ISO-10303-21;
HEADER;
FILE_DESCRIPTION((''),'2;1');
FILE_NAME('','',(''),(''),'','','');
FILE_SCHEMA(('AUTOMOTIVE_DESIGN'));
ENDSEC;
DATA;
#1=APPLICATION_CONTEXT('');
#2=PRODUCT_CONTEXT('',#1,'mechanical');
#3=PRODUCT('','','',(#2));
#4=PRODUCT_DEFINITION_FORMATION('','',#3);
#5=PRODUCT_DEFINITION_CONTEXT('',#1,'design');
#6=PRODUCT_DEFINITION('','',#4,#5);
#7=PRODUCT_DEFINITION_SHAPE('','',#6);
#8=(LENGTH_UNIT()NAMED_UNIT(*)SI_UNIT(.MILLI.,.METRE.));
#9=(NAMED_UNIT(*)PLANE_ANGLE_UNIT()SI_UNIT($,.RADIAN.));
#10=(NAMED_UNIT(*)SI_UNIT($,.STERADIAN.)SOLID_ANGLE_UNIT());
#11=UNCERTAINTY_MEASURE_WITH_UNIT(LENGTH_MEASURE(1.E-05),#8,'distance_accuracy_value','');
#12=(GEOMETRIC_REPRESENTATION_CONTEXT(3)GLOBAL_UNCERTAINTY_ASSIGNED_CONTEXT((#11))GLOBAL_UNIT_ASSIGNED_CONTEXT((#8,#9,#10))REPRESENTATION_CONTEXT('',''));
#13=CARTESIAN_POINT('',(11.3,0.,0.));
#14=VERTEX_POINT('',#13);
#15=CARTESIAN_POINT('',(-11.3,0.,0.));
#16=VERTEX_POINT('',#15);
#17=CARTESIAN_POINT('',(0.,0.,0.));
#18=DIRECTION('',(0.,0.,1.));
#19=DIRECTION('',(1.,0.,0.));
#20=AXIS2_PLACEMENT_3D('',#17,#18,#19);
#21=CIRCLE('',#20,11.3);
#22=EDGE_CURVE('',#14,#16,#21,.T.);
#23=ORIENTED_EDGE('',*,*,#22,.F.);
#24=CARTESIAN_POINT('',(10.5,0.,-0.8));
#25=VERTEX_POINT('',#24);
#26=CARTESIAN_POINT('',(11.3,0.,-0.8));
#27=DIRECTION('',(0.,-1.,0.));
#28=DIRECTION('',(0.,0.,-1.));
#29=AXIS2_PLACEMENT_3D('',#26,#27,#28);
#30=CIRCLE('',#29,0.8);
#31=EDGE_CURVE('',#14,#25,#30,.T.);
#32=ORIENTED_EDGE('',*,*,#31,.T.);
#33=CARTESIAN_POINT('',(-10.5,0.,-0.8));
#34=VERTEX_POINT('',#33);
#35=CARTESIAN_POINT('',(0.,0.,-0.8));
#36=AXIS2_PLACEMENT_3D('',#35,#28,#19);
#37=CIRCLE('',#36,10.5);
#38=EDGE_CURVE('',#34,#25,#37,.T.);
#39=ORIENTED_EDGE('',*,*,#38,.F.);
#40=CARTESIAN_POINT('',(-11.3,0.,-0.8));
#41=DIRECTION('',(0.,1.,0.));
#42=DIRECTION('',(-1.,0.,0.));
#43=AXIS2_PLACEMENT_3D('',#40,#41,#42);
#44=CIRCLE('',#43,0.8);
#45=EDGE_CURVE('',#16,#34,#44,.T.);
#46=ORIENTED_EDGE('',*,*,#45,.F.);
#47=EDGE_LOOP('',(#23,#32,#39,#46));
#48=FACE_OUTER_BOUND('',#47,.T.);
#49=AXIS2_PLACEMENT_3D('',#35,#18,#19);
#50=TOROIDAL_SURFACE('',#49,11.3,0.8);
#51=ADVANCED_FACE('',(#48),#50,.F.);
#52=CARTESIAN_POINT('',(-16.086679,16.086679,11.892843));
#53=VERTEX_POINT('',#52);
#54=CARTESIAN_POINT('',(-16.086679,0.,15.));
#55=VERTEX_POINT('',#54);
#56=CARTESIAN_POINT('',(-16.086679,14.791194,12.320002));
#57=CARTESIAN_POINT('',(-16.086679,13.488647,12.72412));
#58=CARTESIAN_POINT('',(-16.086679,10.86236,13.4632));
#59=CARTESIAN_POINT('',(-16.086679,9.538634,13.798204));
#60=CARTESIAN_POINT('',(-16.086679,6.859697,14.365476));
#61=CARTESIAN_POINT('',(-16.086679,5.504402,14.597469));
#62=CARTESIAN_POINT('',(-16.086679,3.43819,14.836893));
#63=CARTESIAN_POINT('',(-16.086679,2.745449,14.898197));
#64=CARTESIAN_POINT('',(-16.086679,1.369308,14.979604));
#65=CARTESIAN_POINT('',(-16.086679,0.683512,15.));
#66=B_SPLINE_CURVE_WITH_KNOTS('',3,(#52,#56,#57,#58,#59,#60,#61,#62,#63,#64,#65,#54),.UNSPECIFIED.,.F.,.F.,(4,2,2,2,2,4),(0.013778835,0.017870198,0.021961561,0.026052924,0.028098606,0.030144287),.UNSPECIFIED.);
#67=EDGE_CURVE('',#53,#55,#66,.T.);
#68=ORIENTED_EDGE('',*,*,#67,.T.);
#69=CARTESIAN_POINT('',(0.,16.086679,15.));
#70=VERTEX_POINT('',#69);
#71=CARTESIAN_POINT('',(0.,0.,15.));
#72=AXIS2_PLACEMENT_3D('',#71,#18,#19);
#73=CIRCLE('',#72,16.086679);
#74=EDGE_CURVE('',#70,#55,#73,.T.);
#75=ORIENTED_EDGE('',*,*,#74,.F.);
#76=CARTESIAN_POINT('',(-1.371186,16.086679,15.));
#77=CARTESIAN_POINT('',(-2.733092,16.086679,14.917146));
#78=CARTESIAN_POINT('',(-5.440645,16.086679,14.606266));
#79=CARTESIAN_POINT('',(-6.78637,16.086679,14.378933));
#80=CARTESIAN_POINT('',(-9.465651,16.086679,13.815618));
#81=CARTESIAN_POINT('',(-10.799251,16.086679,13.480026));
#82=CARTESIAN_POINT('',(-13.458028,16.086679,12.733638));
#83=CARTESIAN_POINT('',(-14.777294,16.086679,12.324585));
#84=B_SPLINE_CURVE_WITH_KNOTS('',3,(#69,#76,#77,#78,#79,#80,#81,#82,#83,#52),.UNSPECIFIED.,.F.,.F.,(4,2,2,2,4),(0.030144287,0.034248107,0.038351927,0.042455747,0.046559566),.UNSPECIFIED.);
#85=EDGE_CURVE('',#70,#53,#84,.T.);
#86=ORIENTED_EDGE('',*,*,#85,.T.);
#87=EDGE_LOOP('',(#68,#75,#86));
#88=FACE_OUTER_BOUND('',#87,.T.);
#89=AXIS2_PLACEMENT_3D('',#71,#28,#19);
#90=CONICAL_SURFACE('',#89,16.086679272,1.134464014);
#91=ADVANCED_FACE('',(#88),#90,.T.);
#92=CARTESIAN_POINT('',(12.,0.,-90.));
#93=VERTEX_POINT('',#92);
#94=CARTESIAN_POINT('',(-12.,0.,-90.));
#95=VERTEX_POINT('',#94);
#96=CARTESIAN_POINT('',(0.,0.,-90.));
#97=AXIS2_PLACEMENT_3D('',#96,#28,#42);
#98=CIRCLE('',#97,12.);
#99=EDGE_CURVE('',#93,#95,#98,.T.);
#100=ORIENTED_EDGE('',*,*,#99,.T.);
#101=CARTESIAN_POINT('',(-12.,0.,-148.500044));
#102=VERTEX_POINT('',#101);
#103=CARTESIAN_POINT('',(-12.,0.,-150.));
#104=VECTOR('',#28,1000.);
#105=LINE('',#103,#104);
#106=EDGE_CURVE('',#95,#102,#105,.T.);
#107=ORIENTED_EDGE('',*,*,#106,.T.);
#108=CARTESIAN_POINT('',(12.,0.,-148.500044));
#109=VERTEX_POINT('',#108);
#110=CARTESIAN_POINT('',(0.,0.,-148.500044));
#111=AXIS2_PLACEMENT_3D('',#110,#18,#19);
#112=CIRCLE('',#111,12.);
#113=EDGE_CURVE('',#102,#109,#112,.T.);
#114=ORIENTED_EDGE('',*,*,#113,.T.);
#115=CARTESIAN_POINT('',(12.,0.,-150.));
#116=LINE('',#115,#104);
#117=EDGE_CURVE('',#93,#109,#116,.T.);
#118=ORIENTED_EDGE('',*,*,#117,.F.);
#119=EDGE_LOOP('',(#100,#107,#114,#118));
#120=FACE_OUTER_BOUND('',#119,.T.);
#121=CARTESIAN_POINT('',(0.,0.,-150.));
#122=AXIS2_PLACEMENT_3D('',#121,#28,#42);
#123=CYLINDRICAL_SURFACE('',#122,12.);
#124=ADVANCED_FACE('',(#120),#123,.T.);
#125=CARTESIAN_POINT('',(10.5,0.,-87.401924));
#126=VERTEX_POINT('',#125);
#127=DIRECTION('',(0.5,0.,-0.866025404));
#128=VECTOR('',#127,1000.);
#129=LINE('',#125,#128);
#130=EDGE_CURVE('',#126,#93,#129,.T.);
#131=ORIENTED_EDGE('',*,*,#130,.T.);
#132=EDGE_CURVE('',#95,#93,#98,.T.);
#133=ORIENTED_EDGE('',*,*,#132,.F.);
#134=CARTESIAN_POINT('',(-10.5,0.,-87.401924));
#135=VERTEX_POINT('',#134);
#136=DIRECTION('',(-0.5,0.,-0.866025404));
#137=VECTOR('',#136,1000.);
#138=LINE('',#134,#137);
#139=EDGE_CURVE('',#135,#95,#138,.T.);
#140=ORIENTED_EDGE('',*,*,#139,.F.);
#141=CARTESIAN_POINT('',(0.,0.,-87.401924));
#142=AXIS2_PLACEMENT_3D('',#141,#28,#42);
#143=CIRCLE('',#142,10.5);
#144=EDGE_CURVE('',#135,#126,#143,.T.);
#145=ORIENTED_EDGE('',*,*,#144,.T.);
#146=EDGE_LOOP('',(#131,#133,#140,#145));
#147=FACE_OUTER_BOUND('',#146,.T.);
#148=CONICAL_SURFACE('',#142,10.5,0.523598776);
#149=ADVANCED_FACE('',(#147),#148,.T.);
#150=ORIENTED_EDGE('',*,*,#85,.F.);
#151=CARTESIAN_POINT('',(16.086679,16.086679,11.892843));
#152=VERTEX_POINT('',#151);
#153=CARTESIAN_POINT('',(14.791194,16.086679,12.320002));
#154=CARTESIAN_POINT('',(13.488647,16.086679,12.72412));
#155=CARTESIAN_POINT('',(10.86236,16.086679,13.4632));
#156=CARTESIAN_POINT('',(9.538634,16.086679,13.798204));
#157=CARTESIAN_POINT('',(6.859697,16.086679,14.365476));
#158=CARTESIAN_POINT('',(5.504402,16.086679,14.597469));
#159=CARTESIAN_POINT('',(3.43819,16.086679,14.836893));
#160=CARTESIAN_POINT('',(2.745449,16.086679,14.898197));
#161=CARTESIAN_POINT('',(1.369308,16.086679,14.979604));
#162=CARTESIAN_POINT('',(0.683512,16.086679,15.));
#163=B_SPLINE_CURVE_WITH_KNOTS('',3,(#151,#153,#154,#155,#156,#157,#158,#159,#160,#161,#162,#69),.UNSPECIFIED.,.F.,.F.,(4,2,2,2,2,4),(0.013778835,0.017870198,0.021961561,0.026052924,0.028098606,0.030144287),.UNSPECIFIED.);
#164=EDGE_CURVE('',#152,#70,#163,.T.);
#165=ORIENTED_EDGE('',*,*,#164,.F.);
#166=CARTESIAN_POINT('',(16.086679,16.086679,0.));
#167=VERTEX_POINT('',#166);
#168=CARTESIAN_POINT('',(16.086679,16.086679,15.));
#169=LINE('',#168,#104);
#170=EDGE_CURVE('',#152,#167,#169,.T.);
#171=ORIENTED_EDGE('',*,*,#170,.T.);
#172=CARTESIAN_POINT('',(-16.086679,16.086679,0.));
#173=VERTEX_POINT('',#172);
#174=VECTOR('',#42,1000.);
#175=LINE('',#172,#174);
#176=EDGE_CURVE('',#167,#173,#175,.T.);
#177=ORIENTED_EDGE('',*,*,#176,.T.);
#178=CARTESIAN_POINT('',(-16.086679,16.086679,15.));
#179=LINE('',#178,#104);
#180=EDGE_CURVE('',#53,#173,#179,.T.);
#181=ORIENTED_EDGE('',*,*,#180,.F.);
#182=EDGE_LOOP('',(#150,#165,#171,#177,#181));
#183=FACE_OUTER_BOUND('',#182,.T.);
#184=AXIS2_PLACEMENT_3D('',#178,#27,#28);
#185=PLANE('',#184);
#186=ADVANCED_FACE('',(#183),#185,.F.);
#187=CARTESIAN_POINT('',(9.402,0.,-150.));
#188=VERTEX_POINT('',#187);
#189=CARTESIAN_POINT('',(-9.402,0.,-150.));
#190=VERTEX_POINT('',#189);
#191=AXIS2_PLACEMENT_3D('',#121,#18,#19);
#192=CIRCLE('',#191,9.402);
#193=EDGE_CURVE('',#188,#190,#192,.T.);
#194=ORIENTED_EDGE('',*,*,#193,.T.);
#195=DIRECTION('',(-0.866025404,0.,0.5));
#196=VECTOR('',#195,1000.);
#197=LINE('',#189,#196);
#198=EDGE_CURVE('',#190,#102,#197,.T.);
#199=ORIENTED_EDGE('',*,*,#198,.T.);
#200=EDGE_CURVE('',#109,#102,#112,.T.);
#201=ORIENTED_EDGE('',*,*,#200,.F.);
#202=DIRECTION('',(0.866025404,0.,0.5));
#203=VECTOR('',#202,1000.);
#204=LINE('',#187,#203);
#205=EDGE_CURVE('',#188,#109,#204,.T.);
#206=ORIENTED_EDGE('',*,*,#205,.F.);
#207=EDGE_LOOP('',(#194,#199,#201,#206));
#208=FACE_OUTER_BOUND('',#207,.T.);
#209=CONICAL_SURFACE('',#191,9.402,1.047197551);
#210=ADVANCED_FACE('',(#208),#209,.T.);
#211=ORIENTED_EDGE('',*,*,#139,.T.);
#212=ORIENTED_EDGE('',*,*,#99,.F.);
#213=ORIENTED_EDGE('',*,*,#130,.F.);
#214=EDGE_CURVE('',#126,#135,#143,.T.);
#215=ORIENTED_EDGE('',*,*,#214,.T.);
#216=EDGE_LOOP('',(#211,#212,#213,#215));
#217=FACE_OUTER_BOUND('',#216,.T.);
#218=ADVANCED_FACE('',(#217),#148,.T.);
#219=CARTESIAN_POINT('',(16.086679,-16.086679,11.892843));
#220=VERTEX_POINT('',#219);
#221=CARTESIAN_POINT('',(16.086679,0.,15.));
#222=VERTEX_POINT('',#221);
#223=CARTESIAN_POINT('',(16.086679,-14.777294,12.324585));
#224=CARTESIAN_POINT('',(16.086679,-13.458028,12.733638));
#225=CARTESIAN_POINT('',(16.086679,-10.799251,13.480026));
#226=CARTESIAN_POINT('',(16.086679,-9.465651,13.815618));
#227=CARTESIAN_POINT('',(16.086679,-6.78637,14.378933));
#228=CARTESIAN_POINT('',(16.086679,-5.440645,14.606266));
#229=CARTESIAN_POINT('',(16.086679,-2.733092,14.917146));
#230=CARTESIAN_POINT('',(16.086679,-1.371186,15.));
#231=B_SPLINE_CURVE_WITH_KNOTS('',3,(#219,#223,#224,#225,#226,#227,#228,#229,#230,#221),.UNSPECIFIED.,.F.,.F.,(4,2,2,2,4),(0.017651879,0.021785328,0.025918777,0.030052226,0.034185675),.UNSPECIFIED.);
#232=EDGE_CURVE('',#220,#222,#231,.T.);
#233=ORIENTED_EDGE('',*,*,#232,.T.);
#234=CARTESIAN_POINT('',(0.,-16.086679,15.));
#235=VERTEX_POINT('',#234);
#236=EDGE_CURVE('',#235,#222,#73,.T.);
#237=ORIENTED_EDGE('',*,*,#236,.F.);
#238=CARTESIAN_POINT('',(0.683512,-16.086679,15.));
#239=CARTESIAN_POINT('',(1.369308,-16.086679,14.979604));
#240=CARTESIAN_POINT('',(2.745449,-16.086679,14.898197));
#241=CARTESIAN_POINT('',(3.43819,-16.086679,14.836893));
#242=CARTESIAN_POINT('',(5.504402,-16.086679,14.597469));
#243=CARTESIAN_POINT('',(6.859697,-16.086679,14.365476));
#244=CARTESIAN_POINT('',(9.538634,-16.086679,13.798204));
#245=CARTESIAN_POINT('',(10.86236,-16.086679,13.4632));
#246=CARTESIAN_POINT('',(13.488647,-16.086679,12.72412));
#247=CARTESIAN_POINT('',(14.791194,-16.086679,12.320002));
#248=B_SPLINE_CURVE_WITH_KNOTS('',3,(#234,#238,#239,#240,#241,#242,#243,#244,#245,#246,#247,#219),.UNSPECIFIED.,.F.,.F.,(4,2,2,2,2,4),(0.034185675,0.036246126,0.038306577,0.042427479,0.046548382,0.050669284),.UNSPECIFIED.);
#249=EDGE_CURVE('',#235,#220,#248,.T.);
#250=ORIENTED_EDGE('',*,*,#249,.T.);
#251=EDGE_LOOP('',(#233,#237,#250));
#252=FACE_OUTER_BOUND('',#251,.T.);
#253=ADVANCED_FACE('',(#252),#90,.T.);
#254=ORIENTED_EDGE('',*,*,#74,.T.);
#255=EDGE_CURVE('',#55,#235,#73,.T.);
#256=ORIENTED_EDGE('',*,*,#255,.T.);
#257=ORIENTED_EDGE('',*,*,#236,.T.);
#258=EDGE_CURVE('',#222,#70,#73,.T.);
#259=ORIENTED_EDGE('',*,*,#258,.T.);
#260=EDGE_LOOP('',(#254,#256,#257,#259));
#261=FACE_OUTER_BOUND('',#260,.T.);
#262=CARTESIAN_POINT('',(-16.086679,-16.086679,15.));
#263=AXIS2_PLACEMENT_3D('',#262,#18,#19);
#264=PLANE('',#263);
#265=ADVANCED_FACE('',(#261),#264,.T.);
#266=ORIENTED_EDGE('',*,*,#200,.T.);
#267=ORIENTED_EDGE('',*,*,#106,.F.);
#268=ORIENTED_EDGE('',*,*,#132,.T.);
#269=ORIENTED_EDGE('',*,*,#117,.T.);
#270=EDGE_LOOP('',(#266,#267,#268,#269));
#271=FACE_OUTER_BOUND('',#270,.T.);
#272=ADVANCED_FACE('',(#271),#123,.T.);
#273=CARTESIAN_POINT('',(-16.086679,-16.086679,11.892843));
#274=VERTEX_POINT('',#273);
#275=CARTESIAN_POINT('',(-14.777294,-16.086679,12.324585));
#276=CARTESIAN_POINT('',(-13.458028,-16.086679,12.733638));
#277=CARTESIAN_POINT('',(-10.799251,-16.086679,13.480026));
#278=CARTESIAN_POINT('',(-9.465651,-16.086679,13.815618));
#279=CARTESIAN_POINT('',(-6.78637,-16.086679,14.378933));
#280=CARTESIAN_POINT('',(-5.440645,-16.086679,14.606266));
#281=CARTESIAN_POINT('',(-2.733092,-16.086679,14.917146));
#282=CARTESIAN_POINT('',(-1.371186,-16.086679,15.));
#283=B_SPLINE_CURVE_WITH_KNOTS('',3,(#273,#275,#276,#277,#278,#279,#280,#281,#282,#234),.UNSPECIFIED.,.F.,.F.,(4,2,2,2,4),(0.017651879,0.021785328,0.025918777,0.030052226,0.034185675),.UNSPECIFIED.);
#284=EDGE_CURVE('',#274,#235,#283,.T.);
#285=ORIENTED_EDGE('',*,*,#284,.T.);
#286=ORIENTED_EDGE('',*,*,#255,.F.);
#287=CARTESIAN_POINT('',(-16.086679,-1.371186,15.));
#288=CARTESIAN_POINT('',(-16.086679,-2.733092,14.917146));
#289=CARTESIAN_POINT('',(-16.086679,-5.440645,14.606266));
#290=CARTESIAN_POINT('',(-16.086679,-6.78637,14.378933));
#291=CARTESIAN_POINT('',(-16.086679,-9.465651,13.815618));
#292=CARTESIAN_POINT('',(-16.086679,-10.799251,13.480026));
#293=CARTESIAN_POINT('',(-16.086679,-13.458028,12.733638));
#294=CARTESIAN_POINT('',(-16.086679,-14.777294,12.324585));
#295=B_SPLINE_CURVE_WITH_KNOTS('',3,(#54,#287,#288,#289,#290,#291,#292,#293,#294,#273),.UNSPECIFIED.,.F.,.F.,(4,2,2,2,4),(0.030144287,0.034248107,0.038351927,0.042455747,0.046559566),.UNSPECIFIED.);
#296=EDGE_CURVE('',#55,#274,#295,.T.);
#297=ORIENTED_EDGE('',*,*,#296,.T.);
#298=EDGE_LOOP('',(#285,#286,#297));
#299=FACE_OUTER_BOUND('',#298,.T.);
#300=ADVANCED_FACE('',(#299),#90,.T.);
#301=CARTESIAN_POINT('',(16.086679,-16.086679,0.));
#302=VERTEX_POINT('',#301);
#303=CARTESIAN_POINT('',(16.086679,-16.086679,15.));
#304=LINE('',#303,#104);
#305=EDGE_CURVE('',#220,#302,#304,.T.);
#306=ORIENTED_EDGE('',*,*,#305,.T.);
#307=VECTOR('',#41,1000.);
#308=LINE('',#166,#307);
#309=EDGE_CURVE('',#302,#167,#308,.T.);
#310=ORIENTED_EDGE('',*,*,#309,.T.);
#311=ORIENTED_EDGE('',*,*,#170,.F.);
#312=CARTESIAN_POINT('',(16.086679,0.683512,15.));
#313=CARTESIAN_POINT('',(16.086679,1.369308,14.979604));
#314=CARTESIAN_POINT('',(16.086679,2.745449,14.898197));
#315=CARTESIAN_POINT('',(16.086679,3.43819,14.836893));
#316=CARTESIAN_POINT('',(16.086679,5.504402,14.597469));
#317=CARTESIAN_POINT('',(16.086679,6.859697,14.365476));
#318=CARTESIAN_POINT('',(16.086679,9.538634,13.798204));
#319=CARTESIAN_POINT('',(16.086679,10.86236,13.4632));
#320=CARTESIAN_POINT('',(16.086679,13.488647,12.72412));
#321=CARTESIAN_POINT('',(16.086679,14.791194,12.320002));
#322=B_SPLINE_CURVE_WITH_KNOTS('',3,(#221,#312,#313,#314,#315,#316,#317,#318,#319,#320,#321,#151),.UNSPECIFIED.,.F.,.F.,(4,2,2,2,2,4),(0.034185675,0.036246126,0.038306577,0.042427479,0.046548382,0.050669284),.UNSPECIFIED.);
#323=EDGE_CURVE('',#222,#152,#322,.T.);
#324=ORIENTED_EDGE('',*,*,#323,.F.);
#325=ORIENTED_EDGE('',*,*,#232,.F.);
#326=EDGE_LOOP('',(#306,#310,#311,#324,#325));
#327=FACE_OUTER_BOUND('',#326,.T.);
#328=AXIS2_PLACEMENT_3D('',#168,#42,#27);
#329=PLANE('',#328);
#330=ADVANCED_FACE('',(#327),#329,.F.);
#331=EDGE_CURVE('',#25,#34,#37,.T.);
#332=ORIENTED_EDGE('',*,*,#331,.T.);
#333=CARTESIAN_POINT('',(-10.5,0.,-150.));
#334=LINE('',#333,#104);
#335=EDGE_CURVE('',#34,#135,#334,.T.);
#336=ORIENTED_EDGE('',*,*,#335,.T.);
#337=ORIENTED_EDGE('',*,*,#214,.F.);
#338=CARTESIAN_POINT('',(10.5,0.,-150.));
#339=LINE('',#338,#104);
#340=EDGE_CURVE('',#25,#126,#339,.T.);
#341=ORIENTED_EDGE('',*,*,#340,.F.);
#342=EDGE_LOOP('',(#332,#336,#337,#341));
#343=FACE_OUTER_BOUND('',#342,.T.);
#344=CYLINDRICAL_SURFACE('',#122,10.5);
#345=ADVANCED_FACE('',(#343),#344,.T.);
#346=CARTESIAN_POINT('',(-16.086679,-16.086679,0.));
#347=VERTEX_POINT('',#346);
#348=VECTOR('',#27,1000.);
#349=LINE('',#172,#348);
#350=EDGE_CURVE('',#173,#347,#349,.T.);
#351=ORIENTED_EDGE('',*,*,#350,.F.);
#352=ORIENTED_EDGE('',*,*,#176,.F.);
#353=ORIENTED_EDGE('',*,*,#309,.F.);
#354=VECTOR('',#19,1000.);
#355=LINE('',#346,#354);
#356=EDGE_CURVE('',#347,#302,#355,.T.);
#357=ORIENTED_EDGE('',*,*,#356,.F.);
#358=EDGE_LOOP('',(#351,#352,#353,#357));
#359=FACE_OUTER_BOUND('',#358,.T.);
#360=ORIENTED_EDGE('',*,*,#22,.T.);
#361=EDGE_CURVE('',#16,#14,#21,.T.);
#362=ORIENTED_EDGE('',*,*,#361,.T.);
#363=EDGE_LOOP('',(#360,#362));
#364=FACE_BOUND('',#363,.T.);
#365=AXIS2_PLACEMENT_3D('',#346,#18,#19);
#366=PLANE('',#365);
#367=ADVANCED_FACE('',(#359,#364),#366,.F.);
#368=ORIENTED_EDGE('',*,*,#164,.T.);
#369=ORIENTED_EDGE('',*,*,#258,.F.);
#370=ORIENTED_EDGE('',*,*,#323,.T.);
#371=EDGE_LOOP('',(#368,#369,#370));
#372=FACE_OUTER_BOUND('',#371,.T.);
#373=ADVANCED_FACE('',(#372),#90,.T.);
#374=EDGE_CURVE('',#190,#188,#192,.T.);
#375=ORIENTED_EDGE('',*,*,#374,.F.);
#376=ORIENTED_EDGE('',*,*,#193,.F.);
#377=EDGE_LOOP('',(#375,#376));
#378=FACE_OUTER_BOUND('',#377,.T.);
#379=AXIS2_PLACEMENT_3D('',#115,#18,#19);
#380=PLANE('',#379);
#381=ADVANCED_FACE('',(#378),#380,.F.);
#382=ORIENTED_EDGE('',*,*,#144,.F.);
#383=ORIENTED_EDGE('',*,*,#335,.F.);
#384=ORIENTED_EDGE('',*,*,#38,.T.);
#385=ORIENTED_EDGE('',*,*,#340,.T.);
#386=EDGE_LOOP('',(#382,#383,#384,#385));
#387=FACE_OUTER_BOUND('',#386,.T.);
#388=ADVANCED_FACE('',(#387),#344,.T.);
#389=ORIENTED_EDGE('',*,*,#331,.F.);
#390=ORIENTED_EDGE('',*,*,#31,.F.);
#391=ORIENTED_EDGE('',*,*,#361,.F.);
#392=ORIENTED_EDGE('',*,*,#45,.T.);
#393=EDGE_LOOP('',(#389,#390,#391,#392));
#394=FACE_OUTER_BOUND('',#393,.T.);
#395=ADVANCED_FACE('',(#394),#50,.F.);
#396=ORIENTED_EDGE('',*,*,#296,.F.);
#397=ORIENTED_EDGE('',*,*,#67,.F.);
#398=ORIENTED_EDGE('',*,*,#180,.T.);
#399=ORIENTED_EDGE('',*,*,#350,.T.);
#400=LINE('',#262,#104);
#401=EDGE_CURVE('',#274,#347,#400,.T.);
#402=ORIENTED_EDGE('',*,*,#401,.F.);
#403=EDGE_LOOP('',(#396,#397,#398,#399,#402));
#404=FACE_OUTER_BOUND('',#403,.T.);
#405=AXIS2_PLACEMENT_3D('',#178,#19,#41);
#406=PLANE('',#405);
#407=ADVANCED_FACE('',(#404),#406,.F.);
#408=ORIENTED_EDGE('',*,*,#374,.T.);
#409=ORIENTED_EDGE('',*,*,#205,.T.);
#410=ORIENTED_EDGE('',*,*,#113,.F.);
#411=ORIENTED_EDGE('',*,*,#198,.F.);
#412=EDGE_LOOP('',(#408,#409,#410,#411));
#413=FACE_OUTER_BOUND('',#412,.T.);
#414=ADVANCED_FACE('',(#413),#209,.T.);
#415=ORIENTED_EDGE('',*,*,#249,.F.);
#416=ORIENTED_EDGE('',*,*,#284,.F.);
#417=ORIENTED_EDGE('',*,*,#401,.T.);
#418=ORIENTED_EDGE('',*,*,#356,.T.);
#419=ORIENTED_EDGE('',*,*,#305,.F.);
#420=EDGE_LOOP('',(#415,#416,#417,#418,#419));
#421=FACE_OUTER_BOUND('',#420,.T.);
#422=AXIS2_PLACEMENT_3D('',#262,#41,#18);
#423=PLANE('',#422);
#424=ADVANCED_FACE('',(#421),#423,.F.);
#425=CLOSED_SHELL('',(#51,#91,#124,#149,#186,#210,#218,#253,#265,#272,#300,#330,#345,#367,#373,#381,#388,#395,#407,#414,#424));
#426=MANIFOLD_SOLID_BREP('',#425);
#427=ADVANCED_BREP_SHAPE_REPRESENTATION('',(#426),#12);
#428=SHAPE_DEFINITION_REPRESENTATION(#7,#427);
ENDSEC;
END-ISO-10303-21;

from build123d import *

# Parameters (mm, degrees)
SKETCH1_W          = 32.173358544
SKETCH1_H          = 32.173358544
BASE_EXTRUDE_DEPTH = 15
SKETCH4_OUTSIDE_W  = 164.92
SKETCH4_OUTSIDE_H  = 164.92
SKETCH4_OUTSIDE_R  = 16.086679272
CUT_EXTRUDE1_DEPTH = 28.25
CUT_EXTRUDE1_DRAFT = -65
FILLET1_R          = 0.8


with BuildPart() as part:
    # Sketch1 → Base-Extrude (new body)
    with BuildSketch(Plane.XY):
        Rectangle(SKETCH1_W, SKETCH1_H)
    extrude(amount=BASE_EXTRUDE_DEPTH)


with BuildPart() as cut_extrude1_tool:
    # Sketch4 outside → Cut-Extrude1 (with draft: the straight prism first)
    with BuildSketch(Plane.XY.offset(15)):
        Rectangle(SKETCH4_OUTSIDE_W, SKETCH4_OUTSIDE_H)
        Circle(SKETCH4_OUTSIDE_R, mode=Mode.SUBTRACT)
    extrude(amount=-CUT_EXTRUDE1_DEPTH)
    # Cut-Extrude1: the draft: its side faces are tilted about the plane it starts from
    cut_extrude1_sides = [cut_extrude1_tool.faces().sort_by_distance(p)[0] for p in [
        (0, -82.46, 0.875),
        (82.46, 0, 0.875),
        (0, 82.46, 0.875),
        (-82.46, 0, 0.875),
        (-16.086679272, 0, 0.875),
    ]]
    draft(cut_extrude1_sides, Plane.XY.offset(15), CUT_EXTRUDE1_DRAFT)


with BuildPart() as part_1:
    add(part.part)

    # Cut-Extrude1: cut by cut_extrude1_tool
    add(cut_extrude1_tool.part, mode=Mode.SUBTRACT)

    # Sketch2 → Boss-Revolve1 (revolve)
    with BuildSketch(Plane(origin=(0, 0, 0), x_dir=(1, 0, 0), z_dir=(0, 1, 0)), mode=Mode.PRIVATE) as boss_revolve1_sk:
        Polygon((0, 0), (10.5, 0), (10.5, 87.401923789), (12, 90), (12, 150), (0, 150), align=None)
    revolve(boss_revolve1_sk.sketch.rotate(Axis((0, 0, -150), (0, 0, 1)), 180), axis=Axis((0, 0, -150), (0, 0, 1)))

    # Fillet1
    fillet1_edges = [part_1.edges().sort_by_distance(p)[0] for p in [
        (10.5, 0, 0),
    ]]
    fillet(fillet1_edges, radius=FILLET1_R)

    # Sketch3 → Cut-Revolve1 (revolve, cut)
    with BuildSketch(Plane(origin=(0, 0, 0), x_dir=(1, 0, 0), z_dir=(0, 1, 0))):
        Polygon((9.402, 150), (12, 151.499955999), (12, 148.500044001), align=None)
    revolve(axis=Axis((0, 0, 0), (0, 0, -1)), mode=Mode.SUBTRACT)


solid = part_1.part
